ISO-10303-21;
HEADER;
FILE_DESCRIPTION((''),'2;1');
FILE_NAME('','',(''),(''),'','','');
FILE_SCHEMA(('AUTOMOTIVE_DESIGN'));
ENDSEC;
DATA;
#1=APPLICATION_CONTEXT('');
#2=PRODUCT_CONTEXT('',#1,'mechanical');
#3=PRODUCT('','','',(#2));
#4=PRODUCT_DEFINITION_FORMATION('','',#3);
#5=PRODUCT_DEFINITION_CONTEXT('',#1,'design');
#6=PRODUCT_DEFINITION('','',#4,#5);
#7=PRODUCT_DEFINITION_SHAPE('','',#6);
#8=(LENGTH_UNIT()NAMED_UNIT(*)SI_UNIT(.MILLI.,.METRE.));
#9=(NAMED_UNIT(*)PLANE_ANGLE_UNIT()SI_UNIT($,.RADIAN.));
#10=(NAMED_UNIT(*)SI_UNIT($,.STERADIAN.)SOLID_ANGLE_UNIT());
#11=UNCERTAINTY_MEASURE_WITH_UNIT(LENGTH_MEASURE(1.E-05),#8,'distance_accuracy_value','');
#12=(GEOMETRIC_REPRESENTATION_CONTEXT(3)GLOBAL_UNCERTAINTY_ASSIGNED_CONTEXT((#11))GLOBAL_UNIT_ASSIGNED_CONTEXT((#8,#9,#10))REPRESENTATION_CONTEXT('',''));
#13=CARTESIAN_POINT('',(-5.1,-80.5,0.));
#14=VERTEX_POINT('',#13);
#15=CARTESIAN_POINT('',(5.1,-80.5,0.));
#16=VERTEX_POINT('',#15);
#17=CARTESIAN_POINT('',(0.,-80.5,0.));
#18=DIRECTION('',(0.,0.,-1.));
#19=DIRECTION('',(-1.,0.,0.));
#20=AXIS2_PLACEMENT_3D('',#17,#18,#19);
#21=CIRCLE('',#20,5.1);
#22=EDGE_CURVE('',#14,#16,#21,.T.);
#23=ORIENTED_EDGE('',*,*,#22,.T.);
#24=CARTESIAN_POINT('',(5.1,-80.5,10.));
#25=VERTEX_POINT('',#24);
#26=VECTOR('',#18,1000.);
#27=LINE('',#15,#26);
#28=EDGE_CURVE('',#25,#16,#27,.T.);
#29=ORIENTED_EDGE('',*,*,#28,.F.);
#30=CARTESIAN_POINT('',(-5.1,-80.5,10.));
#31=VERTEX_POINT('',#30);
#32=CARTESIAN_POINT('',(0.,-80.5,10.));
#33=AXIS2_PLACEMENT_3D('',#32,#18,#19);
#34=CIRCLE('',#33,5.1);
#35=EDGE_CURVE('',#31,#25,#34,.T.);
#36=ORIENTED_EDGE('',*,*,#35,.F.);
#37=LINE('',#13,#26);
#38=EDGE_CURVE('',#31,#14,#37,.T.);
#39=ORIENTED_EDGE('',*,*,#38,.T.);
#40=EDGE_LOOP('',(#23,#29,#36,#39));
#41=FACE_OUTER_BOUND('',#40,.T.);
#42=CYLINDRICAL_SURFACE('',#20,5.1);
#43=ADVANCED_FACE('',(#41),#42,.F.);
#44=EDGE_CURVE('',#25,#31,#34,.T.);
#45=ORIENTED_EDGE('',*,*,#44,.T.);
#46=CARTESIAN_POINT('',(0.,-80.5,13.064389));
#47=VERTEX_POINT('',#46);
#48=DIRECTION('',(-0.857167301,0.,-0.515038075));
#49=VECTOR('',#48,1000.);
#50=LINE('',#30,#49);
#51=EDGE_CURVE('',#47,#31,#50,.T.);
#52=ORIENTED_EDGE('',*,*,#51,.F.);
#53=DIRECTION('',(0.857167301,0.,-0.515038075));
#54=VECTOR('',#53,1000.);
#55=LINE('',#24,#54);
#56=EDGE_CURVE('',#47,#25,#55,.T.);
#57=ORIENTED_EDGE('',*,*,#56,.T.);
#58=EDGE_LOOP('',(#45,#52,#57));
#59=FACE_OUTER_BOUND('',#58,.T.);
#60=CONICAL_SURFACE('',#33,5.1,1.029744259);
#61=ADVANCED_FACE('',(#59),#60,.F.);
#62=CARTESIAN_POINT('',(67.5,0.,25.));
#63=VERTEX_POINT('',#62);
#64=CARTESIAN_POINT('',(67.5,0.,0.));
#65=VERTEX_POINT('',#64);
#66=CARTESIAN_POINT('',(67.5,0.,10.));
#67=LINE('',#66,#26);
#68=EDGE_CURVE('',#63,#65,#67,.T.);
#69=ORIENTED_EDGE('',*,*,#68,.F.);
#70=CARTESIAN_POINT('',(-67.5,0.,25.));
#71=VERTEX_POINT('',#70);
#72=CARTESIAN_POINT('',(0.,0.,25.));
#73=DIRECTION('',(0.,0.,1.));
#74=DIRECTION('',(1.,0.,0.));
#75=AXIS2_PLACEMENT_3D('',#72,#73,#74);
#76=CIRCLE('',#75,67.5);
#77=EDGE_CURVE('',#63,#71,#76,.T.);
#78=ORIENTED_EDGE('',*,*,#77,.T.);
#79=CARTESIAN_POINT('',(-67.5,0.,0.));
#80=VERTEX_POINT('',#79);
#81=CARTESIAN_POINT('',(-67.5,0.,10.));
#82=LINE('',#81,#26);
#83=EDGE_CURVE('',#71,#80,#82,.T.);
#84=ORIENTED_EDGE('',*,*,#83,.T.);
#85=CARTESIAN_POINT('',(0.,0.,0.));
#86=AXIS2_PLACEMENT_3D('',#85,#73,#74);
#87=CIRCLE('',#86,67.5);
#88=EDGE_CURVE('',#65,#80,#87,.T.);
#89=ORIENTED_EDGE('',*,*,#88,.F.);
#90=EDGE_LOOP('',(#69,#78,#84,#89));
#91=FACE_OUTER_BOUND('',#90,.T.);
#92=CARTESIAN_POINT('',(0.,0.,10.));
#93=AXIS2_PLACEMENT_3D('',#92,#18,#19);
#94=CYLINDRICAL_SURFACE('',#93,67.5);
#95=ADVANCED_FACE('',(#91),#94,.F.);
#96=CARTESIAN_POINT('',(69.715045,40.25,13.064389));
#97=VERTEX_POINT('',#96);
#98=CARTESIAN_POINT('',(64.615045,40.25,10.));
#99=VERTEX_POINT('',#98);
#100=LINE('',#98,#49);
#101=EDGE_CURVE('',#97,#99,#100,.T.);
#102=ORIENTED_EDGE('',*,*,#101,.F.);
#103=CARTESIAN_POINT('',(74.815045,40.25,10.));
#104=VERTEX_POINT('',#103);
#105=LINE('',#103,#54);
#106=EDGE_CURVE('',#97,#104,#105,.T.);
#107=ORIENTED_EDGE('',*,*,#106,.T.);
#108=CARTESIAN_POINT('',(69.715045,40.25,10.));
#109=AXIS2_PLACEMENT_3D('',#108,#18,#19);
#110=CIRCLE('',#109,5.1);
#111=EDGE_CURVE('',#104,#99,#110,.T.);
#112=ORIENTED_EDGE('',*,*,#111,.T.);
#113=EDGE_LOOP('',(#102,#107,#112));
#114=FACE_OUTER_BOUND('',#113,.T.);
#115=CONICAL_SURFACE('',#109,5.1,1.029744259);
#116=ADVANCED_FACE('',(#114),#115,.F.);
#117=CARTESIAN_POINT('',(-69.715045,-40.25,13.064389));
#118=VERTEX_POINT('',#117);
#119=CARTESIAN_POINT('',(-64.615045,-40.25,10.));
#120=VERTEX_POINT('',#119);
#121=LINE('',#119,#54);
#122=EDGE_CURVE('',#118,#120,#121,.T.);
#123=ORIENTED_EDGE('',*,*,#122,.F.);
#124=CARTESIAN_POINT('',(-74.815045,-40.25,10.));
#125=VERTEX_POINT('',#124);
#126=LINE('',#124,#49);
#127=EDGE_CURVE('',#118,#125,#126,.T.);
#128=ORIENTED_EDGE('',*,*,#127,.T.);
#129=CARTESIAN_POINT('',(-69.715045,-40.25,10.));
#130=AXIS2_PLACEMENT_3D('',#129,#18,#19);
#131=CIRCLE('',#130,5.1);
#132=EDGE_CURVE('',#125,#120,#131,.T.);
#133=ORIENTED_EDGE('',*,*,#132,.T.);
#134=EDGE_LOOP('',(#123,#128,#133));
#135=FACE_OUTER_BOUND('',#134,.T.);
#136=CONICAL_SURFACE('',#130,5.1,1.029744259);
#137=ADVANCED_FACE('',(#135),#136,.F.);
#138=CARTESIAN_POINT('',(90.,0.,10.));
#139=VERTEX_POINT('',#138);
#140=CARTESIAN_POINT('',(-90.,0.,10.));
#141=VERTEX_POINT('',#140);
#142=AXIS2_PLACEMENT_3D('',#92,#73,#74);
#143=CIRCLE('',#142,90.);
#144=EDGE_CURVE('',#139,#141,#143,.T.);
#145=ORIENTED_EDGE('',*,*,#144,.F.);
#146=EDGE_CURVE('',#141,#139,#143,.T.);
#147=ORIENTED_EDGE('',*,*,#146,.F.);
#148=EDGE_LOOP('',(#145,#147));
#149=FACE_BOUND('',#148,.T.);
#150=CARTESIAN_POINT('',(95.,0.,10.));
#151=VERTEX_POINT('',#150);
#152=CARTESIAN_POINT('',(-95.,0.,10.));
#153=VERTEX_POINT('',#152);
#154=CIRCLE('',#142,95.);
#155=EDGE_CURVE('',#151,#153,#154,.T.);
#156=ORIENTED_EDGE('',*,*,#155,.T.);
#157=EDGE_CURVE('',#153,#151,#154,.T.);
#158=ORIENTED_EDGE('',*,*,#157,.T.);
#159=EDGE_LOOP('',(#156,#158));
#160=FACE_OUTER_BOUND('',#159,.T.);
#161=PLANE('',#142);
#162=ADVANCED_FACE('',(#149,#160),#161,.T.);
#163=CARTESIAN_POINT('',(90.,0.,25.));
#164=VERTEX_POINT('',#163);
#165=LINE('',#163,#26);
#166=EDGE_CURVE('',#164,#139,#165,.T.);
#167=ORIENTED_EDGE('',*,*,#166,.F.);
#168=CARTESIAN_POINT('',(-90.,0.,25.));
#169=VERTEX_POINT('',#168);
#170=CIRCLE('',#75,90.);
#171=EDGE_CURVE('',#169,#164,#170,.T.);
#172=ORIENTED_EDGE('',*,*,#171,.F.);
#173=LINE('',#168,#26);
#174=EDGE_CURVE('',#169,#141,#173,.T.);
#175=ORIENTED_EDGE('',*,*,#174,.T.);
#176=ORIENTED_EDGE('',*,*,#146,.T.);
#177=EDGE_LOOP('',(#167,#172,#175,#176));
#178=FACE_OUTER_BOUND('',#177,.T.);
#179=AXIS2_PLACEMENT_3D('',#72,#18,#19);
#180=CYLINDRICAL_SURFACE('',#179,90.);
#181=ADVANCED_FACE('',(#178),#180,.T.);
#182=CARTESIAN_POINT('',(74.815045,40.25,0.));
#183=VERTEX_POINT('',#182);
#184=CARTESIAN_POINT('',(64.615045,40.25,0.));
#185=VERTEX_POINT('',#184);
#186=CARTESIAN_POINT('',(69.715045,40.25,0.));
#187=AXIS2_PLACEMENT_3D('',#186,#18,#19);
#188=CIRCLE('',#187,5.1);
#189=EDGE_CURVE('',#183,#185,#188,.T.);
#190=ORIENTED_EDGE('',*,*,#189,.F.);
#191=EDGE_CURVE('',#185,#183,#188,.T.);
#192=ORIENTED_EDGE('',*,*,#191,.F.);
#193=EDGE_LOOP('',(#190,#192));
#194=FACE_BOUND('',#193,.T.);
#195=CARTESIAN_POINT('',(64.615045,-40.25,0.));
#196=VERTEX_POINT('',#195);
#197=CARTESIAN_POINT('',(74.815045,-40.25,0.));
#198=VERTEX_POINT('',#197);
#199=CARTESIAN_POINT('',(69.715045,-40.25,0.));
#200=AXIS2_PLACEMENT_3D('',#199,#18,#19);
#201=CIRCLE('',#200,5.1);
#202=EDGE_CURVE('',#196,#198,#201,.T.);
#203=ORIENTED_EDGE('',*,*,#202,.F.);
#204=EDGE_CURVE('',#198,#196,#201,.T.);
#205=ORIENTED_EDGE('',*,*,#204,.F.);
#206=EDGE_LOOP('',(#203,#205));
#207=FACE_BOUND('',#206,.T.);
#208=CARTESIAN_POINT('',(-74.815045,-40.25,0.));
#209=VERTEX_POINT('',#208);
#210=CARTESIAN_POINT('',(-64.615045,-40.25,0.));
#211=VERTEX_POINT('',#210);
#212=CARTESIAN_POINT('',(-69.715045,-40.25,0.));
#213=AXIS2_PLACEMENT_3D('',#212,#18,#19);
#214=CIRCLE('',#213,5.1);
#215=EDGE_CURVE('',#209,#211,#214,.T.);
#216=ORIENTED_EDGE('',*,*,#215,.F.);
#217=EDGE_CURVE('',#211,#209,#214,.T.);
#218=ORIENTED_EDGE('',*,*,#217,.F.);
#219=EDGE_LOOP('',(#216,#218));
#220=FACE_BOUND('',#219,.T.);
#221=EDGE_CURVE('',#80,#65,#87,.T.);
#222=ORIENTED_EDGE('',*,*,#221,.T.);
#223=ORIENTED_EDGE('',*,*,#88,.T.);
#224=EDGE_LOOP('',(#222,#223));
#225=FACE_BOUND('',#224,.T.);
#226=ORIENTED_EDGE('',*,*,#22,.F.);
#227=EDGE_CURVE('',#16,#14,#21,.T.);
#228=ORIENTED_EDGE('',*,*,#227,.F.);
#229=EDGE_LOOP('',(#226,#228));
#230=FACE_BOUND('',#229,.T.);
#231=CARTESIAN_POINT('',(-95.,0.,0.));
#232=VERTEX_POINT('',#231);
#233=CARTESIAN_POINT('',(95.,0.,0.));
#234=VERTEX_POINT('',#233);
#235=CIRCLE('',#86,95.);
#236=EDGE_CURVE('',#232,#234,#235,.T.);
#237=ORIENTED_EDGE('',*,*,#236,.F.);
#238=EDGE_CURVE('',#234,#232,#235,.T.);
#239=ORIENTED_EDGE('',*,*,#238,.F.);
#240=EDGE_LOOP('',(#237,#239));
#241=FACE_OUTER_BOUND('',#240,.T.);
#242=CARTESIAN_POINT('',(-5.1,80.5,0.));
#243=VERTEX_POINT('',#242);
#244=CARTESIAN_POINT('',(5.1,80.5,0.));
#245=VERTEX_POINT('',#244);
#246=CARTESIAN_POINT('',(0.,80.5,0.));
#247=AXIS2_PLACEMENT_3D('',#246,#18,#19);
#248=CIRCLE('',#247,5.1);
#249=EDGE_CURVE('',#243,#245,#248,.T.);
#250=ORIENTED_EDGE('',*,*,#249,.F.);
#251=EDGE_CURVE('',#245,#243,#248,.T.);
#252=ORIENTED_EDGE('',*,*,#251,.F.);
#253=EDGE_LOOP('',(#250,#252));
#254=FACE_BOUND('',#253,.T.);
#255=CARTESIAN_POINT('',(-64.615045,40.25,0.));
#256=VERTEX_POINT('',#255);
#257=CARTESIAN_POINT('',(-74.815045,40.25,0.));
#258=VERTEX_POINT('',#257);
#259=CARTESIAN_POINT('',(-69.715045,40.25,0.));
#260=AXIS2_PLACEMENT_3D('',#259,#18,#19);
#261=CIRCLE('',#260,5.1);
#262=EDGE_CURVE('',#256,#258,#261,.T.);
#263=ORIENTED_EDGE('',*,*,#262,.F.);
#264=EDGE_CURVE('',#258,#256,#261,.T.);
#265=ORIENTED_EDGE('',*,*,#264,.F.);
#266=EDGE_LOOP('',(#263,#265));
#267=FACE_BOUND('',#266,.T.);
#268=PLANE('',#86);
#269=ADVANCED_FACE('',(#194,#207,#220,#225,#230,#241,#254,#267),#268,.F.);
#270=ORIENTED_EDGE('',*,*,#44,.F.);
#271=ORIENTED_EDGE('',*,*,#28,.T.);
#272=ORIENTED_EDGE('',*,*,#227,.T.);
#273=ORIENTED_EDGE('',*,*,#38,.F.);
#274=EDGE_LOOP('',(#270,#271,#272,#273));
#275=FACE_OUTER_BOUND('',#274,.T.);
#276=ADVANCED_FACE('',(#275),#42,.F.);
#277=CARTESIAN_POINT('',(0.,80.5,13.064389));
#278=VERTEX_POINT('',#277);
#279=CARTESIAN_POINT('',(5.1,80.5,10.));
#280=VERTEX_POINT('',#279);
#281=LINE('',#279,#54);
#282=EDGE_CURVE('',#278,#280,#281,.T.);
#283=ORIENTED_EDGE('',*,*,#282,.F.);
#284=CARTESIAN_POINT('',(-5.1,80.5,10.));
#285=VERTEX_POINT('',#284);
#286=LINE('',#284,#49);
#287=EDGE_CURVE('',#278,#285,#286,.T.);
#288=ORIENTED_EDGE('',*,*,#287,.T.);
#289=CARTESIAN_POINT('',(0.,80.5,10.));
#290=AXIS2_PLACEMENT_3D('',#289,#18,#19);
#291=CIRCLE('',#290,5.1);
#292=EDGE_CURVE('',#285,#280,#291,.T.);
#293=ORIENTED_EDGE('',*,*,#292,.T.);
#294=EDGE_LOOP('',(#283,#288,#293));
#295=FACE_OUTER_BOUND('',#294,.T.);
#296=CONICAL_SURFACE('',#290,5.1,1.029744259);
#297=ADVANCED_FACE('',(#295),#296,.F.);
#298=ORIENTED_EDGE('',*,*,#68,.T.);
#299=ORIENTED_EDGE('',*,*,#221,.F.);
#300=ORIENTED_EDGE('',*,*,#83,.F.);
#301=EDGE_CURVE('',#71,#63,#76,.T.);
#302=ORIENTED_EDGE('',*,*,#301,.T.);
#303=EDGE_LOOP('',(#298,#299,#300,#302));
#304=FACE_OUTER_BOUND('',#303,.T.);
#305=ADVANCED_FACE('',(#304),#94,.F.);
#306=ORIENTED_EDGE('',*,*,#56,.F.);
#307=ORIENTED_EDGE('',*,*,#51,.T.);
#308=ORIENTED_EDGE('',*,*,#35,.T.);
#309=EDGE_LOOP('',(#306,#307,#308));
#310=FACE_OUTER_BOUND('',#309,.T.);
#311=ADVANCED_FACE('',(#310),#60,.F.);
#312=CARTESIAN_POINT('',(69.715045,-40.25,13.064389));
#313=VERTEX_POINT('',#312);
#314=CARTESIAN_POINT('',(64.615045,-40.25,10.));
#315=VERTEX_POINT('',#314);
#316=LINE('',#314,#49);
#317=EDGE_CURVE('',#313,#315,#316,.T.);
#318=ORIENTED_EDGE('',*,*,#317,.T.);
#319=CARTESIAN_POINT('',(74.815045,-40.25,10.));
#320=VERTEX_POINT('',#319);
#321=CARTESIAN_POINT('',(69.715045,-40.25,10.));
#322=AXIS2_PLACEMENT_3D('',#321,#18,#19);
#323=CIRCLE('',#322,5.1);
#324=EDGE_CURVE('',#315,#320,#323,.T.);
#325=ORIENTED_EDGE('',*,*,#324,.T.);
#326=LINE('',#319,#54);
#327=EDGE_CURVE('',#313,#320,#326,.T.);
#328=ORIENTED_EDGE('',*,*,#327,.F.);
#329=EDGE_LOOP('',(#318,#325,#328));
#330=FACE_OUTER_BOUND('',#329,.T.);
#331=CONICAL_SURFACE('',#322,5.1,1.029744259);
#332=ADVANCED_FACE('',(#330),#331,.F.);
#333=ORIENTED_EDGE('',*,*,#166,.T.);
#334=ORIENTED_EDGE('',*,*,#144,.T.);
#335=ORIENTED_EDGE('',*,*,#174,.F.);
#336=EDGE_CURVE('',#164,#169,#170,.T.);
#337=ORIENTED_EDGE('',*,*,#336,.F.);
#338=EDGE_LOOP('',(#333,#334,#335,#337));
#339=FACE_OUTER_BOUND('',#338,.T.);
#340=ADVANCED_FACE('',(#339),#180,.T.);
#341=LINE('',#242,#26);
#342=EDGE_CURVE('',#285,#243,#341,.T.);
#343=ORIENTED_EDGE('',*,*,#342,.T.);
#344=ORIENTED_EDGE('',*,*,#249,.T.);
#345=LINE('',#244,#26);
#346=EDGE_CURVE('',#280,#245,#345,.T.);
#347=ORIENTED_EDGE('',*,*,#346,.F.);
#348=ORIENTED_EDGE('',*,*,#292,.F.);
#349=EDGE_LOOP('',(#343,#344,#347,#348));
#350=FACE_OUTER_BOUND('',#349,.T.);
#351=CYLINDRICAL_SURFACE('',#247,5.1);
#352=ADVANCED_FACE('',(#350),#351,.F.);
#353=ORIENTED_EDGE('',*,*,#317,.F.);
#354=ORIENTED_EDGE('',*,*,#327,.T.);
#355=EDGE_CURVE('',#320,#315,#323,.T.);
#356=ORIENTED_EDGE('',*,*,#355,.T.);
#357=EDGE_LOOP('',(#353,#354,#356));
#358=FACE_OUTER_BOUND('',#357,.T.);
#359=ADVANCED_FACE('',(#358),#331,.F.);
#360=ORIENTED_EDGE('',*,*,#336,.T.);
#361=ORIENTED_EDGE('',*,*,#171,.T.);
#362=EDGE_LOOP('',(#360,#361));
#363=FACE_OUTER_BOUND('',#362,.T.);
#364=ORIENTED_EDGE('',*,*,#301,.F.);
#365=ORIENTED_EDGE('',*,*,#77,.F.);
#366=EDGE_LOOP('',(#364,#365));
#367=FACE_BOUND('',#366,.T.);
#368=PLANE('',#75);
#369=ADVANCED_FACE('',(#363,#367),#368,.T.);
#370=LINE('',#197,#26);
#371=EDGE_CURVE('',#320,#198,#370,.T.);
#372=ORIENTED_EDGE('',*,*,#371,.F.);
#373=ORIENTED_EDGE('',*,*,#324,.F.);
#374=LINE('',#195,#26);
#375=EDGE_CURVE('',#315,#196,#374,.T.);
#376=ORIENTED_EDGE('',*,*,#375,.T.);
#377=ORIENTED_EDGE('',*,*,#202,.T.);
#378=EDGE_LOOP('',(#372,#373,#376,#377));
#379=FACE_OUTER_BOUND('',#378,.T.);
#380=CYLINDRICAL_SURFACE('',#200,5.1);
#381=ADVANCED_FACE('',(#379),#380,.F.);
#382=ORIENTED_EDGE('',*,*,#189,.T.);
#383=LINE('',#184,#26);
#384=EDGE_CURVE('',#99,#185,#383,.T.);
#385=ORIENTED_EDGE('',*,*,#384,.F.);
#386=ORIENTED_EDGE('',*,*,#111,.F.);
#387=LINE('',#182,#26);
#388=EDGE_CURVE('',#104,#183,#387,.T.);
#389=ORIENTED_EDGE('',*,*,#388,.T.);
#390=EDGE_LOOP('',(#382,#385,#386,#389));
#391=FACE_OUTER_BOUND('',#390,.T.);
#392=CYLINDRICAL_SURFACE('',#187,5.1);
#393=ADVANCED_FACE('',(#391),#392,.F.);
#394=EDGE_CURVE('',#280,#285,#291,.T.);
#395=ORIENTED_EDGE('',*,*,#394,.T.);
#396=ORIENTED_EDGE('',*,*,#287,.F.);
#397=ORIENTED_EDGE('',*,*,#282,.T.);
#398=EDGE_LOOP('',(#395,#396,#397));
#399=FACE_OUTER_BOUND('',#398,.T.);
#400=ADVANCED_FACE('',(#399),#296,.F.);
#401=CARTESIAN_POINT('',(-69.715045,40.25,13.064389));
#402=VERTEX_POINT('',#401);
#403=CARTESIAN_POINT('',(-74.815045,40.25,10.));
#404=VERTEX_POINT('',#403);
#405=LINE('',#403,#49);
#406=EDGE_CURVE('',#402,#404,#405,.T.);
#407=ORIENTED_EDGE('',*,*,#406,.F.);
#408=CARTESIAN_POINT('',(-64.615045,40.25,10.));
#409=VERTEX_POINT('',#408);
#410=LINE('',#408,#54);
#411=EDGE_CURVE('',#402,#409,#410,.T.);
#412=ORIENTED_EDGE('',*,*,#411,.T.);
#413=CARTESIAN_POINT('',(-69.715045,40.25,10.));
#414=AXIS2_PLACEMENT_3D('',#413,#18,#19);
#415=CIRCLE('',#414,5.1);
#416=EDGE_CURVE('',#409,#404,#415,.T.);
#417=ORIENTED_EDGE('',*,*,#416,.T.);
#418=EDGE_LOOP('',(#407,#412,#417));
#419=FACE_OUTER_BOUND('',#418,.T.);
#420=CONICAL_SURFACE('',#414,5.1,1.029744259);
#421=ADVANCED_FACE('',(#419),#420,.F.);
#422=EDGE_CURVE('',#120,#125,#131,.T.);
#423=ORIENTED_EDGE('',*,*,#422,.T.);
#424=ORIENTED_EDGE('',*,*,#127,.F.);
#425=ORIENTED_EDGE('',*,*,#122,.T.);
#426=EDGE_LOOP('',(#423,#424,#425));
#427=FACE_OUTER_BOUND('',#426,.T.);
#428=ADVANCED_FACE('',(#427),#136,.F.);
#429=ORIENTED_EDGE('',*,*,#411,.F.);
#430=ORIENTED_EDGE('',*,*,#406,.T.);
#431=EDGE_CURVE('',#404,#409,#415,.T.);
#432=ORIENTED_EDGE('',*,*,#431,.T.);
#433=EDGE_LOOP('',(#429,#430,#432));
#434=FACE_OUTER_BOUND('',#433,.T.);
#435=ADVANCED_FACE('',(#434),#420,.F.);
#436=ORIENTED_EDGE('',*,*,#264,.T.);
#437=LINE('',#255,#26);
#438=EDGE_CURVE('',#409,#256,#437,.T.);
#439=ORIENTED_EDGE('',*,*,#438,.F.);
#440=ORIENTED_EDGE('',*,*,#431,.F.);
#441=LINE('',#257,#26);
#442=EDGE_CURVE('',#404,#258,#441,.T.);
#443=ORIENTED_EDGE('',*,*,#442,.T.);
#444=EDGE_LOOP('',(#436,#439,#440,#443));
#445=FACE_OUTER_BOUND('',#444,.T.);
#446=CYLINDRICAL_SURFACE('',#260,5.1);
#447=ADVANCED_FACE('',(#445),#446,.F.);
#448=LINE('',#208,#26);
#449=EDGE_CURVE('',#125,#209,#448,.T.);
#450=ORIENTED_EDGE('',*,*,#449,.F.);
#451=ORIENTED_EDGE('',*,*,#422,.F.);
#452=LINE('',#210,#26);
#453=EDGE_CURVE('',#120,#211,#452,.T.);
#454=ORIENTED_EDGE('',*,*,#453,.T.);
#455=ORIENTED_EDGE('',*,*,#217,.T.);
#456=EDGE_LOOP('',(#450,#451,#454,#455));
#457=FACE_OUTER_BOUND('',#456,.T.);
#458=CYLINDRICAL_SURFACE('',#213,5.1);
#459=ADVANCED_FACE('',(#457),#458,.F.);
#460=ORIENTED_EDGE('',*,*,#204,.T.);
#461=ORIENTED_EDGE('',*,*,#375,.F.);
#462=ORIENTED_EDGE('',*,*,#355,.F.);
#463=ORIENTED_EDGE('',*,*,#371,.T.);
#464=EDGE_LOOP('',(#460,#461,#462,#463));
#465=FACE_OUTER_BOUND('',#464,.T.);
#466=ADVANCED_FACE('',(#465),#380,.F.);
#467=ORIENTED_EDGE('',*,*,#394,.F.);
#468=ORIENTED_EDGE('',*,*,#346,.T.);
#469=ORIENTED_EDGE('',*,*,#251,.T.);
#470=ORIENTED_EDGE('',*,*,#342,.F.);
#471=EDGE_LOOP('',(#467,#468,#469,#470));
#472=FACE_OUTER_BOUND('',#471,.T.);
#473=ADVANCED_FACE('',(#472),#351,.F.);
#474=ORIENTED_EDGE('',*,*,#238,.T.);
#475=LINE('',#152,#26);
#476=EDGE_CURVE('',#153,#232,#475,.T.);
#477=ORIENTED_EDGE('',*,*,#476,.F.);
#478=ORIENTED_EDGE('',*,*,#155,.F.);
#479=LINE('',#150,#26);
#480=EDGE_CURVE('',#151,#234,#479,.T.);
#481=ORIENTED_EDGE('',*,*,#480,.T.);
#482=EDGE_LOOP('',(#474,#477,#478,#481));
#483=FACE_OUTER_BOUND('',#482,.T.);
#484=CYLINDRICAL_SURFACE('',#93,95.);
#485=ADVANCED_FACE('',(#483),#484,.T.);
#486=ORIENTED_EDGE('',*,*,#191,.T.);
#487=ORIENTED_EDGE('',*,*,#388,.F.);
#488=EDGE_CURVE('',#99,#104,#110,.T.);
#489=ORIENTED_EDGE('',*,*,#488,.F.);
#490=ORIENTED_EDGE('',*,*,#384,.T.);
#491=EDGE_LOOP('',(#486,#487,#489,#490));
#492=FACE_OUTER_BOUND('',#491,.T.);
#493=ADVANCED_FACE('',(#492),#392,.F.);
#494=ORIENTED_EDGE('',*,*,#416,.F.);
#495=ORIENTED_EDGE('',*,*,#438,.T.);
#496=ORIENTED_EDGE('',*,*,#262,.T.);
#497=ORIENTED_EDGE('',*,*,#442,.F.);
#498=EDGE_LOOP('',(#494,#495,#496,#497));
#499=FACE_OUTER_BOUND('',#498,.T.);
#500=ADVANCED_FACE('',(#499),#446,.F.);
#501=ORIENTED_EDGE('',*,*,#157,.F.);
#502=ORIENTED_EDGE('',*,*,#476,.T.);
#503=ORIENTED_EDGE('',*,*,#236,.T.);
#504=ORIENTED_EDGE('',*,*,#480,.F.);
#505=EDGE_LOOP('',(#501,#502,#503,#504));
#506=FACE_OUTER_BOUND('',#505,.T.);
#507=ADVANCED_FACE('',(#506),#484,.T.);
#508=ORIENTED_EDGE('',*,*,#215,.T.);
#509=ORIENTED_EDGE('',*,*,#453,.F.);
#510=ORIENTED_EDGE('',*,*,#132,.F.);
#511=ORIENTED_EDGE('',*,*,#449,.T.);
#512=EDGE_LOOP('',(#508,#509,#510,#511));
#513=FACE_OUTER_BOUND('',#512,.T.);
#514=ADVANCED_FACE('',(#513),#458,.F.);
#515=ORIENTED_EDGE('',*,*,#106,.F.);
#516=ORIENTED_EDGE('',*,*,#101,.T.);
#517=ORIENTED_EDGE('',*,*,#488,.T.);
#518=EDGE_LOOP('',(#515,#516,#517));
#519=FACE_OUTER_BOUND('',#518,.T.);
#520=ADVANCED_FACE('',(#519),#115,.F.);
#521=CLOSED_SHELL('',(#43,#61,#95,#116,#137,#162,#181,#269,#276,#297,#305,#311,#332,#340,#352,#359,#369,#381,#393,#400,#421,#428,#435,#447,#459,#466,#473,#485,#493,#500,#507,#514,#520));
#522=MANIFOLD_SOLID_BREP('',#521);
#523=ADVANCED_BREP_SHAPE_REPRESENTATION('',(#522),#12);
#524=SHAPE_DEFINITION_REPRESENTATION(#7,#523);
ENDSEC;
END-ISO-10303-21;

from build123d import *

# Parameters (mm, degrees)
SKETCH1_R              = 95
SKETCH1_R_2            = 67.5
BOSS_EXTRUDE1_DEPTH    = 10
SKETCH2_R              = 90
SKETCH2_R_2            = 67.5
BOSS_EXTRUDE2_DEPTH    = 15
M12_TAPPED_HOLE2_D     = 10.2
M12_TAPPED_HOLE2_DEPTH = 10
M12_TAPPED_HOLE2_TIP   = 3.064389157


with BuildPart() as part:
    # Sketch1 → Boss-Extrude1 (new body)
    with BuildSketch(Plane.XY):
        Circle(SKETCH1_R)
        Circle(SKETCH1_R_2, mode=Mode.SUBTRACT)
    extrude(amount=BOSS_EXTRUDE1_DEPTH)

    # Sketch2 → Boss-Extrude2 (add)
    with BuildSketch(Plane.XY.offset(10)):
        Circle(SKETCH2_R)
        Circle(SKETCH2_R_2, mode=Mode.SUBTRACT)
    extrude(amount=BOSS_EXTRUDE2_DEPTH)

    # M12 Tapped Hole2
    with Locations(Plane(origin=(0, 80.5, 0), x_dir=(-1, 0, 0), z_dir=(0, 0, -1))):
        with Locations((0, 0), (-69.715045005, -40.25), (-69.715045005, -120.75), (0, -161), (69.715045005, -120.75), (69.715045005, -40.25)):
            Hole(M12_TAPPED_HOLE2_D / 2, depth=M12_TAPPED_HOLE2_DEPTH)
            with Locations((0, 0, -(M12_TAPPED_HOLE2_DEPTH + M12_TAPPED_HOLE2_TIP / 2))):  # 118° drill point
                Cone(0, M12_TAPPED_HOLE2_D / 2, M12_TAPPED_HOLE2_TIP, mode=Mode.SUBTRACT)


solid = part.part
